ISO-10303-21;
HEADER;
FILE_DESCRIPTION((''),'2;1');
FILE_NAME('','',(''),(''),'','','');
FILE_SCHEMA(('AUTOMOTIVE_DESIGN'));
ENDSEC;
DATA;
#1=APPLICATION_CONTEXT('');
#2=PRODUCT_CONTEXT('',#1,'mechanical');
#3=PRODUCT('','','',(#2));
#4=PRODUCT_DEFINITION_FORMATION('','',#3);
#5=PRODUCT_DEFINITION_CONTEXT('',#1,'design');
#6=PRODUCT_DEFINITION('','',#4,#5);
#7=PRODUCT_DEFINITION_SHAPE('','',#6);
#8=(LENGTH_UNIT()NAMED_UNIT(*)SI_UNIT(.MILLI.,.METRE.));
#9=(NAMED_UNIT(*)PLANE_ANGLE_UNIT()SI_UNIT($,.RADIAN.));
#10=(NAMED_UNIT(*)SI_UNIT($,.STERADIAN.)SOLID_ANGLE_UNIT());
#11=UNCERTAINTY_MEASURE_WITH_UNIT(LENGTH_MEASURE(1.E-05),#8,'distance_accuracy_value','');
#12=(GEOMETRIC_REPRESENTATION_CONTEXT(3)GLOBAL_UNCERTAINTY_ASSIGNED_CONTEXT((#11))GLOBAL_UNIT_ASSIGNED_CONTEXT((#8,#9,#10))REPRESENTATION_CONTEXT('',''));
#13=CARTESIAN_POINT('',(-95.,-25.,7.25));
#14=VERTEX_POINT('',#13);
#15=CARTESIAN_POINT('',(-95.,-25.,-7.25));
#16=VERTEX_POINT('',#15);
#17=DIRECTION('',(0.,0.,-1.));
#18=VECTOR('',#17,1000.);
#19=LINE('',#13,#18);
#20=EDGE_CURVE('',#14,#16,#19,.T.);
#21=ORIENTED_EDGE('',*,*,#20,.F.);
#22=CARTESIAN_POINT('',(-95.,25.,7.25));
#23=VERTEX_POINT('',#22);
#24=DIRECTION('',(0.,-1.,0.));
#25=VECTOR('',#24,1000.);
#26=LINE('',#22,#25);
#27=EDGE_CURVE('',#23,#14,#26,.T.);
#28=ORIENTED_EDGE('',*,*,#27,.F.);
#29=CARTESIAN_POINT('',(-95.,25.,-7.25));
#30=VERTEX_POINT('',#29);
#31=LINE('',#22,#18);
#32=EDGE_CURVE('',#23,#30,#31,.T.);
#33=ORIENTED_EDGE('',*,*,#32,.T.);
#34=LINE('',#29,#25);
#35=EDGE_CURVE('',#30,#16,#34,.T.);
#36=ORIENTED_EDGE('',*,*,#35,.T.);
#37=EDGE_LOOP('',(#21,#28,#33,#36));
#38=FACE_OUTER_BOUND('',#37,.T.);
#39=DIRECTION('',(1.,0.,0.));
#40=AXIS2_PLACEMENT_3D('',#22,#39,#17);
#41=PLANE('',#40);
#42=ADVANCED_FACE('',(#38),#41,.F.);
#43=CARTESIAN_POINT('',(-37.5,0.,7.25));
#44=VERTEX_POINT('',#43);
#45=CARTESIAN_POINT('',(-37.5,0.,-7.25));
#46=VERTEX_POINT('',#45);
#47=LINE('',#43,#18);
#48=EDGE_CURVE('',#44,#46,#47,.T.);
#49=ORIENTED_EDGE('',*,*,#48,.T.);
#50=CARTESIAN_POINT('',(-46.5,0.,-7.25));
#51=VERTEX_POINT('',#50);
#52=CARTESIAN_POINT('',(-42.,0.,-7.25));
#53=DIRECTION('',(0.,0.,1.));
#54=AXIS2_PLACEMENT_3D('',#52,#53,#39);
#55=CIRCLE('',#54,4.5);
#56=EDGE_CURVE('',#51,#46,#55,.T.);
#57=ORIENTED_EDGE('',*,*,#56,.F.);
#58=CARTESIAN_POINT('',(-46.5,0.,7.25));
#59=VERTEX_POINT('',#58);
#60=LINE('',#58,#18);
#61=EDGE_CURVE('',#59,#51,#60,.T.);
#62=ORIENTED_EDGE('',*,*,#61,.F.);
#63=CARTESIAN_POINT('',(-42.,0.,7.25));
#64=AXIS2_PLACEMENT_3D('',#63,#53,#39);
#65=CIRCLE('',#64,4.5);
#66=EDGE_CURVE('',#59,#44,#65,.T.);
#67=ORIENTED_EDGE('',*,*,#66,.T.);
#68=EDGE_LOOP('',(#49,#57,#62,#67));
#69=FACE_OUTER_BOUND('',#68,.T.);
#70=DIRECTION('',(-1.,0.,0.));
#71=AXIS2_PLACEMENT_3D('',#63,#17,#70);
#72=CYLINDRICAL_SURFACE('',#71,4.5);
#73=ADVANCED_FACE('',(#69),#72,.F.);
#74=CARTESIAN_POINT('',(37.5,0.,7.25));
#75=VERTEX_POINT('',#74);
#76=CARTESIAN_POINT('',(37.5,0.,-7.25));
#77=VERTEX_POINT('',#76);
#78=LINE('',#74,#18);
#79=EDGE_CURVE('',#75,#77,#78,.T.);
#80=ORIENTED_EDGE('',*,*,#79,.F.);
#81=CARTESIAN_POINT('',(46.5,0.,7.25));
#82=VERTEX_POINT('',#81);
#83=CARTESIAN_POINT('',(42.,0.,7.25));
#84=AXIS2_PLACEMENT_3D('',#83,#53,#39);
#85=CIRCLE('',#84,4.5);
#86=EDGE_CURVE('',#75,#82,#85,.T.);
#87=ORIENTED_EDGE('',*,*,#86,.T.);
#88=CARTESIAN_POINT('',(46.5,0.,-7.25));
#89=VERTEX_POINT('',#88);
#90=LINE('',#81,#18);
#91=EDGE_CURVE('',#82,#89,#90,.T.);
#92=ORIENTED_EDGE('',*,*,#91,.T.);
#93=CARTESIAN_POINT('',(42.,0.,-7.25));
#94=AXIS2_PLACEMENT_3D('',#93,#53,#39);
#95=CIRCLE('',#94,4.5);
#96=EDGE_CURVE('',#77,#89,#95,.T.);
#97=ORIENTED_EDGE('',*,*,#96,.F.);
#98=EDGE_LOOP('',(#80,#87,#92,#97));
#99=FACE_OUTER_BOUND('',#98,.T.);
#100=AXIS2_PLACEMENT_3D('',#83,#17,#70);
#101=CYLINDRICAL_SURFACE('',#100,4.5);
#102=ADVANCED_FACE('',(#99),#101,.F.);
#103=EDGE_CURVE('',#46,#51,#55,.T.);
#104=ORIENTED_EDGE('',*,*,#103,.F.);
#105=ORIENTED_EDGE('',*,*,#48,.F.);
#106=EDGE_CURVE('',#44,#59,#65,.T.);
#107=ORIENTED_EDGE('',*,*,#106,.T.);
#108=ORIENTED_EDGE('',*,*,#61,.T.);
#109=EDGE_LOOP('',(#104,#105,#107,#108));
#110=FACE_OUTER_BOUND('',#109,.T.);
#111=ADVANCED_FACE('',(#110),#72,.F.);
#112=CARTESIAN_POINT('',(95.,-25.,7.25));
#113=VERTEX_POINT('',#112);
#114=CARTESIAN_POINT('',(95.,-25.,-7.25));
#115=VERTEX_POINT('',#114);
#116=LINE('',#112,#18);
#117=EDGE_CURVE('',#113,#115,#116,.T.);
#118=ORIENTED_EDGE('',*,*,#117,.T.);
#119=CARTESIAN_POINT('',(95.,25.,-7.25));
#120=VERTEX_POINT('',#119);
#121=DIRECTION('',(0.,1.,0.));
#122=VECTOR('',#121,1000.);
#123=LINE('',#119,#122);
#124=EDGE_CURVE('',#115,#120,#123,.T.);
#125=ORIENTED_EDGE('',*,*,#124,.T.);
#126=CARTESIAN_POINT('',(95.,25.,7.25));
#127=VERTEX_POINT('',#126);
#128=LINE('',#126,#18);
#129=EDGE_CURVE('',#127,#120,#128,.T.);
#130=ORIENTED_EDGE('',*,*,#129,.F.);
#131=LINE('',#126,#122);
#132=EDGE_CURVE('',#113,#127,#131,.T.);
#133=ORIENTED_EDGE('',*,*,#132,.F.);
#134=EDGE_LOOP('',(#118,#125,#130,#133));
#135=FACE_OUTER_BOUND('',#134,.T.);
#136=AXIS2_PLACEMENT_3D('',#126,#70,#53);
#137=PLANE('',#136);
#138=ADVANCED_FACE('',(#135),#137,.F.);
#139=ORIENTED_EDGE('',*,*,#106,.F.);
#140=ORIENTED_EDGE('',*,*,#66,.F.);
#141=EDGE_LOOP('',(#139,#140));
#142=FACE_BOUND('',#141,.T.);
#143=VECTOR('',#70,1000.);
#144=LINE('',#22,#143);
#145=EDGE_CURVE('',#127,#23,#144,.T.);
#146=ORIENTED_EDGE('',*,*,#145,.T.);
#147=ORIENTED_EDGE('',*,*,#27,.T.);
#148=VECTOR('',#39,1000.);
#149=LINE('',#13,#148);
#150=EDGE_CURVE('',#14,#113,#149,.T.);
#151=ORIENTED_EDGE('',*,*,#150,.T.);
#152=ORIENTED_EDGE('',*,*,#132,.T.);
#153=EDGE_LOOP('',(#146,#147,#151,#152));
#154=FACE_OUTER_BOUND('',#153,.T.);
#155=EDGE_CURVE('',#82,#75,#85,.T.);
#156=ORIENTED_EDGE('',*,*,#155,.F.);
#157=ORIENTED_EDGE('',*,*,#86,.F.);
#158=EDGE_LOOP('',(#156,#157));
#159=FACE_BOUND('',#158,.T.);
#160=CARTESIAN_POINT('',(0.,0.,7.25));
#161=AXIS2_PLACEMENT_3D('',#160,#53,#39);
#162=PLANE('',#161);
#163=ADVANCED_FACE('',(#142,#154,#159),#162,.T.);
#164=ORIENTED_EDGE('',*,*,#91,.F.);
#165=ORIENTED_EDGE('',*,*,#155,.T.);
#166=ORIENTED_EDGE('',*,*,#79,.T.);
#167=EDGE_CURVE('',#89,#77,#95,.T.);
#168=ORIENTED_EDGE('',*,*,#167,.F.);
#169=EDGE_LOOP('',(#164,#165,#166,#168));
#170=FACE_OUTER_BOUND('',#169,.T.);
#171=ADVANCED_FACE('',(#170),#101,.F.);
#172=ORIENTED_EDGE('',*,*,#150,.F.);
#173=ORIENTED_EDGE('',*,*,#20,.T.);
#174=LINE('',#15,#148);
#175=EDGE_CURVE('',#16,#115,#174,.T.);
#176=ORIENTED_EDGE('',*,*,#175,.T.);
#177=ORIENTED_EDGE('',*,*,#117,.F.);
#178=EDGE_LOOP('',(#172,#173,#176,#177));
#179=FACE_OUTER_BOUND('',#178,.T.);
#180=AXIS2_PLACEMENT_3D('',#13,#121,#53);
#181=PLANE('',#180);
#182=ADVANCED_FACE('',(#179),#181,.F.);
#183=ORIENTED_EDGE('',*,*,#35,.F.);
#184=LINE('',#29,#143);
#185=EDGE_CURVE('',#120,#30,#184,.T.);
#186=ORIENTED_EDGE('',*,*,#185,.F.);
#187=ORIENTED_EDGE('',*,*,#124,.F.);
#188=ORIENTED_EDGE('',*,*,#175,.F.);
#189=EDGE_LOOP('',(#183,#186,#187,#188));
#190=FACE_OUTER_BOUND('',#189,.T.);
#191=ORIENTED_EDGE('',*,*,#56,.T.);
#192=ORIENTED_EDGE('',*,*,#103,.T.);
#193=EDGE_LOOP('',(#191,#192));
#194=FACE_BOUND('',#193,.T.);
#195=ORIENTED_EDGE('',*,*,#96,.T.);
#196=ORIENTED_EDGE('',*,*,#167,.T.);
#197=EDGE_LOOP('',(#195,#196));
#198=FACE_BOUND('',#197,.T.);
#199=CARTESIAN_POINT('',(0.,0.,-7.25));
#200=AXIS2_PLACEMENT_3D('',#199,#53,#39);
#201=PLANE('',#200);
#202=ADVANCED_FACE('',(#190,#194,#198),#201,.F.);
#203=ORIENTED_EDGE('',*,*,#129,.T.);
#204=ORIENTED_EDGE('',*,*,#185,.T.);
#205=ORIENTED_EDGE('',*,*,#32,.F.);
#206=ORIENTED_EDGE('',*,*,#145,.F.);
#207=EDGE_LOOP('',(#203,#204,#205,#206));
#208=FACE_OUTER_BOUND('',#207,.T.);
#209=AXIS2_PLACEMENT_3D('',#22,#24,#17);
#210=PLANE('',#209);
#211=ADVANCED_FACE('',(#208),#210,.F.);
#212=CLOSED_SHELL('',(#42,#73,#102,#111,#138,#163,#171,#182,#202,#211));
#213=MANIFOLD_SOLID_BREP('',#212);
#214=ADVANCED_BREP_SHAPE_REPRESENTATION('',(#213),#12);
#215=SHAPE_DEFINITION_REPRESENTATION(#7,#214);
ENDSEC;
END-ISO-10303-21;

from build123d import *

# Parameters (mm, degrees)
SKETCH_1_W      = 190
SKETCH_1_H      = 50
SKETCH_1_R      = 4.5
EXTRUDE_1_DEPTH = 7.25


with BuildPart() as part:
    # 草图1 → 凸台-拉伸1 (new, symmetric)
    with BuildSketch(Plane.XY):
        Rectangle(SKETCH_1_W, SKETCH_1_H)
        with Locations(Location((-42, 0, 0), (0, 0, 180))):
            Circle(SKETCH_1_R, mode=Mode.SUBTRACT)
        with Locations(Location((42, 0, 0), (0, 0, 180))):
            Circle(SKETCH_1_R, mode=Mode.SUBTRACT)
    extrude(amount=EXTRUDE_1_DEPTH, both=True)


solid = part.part
